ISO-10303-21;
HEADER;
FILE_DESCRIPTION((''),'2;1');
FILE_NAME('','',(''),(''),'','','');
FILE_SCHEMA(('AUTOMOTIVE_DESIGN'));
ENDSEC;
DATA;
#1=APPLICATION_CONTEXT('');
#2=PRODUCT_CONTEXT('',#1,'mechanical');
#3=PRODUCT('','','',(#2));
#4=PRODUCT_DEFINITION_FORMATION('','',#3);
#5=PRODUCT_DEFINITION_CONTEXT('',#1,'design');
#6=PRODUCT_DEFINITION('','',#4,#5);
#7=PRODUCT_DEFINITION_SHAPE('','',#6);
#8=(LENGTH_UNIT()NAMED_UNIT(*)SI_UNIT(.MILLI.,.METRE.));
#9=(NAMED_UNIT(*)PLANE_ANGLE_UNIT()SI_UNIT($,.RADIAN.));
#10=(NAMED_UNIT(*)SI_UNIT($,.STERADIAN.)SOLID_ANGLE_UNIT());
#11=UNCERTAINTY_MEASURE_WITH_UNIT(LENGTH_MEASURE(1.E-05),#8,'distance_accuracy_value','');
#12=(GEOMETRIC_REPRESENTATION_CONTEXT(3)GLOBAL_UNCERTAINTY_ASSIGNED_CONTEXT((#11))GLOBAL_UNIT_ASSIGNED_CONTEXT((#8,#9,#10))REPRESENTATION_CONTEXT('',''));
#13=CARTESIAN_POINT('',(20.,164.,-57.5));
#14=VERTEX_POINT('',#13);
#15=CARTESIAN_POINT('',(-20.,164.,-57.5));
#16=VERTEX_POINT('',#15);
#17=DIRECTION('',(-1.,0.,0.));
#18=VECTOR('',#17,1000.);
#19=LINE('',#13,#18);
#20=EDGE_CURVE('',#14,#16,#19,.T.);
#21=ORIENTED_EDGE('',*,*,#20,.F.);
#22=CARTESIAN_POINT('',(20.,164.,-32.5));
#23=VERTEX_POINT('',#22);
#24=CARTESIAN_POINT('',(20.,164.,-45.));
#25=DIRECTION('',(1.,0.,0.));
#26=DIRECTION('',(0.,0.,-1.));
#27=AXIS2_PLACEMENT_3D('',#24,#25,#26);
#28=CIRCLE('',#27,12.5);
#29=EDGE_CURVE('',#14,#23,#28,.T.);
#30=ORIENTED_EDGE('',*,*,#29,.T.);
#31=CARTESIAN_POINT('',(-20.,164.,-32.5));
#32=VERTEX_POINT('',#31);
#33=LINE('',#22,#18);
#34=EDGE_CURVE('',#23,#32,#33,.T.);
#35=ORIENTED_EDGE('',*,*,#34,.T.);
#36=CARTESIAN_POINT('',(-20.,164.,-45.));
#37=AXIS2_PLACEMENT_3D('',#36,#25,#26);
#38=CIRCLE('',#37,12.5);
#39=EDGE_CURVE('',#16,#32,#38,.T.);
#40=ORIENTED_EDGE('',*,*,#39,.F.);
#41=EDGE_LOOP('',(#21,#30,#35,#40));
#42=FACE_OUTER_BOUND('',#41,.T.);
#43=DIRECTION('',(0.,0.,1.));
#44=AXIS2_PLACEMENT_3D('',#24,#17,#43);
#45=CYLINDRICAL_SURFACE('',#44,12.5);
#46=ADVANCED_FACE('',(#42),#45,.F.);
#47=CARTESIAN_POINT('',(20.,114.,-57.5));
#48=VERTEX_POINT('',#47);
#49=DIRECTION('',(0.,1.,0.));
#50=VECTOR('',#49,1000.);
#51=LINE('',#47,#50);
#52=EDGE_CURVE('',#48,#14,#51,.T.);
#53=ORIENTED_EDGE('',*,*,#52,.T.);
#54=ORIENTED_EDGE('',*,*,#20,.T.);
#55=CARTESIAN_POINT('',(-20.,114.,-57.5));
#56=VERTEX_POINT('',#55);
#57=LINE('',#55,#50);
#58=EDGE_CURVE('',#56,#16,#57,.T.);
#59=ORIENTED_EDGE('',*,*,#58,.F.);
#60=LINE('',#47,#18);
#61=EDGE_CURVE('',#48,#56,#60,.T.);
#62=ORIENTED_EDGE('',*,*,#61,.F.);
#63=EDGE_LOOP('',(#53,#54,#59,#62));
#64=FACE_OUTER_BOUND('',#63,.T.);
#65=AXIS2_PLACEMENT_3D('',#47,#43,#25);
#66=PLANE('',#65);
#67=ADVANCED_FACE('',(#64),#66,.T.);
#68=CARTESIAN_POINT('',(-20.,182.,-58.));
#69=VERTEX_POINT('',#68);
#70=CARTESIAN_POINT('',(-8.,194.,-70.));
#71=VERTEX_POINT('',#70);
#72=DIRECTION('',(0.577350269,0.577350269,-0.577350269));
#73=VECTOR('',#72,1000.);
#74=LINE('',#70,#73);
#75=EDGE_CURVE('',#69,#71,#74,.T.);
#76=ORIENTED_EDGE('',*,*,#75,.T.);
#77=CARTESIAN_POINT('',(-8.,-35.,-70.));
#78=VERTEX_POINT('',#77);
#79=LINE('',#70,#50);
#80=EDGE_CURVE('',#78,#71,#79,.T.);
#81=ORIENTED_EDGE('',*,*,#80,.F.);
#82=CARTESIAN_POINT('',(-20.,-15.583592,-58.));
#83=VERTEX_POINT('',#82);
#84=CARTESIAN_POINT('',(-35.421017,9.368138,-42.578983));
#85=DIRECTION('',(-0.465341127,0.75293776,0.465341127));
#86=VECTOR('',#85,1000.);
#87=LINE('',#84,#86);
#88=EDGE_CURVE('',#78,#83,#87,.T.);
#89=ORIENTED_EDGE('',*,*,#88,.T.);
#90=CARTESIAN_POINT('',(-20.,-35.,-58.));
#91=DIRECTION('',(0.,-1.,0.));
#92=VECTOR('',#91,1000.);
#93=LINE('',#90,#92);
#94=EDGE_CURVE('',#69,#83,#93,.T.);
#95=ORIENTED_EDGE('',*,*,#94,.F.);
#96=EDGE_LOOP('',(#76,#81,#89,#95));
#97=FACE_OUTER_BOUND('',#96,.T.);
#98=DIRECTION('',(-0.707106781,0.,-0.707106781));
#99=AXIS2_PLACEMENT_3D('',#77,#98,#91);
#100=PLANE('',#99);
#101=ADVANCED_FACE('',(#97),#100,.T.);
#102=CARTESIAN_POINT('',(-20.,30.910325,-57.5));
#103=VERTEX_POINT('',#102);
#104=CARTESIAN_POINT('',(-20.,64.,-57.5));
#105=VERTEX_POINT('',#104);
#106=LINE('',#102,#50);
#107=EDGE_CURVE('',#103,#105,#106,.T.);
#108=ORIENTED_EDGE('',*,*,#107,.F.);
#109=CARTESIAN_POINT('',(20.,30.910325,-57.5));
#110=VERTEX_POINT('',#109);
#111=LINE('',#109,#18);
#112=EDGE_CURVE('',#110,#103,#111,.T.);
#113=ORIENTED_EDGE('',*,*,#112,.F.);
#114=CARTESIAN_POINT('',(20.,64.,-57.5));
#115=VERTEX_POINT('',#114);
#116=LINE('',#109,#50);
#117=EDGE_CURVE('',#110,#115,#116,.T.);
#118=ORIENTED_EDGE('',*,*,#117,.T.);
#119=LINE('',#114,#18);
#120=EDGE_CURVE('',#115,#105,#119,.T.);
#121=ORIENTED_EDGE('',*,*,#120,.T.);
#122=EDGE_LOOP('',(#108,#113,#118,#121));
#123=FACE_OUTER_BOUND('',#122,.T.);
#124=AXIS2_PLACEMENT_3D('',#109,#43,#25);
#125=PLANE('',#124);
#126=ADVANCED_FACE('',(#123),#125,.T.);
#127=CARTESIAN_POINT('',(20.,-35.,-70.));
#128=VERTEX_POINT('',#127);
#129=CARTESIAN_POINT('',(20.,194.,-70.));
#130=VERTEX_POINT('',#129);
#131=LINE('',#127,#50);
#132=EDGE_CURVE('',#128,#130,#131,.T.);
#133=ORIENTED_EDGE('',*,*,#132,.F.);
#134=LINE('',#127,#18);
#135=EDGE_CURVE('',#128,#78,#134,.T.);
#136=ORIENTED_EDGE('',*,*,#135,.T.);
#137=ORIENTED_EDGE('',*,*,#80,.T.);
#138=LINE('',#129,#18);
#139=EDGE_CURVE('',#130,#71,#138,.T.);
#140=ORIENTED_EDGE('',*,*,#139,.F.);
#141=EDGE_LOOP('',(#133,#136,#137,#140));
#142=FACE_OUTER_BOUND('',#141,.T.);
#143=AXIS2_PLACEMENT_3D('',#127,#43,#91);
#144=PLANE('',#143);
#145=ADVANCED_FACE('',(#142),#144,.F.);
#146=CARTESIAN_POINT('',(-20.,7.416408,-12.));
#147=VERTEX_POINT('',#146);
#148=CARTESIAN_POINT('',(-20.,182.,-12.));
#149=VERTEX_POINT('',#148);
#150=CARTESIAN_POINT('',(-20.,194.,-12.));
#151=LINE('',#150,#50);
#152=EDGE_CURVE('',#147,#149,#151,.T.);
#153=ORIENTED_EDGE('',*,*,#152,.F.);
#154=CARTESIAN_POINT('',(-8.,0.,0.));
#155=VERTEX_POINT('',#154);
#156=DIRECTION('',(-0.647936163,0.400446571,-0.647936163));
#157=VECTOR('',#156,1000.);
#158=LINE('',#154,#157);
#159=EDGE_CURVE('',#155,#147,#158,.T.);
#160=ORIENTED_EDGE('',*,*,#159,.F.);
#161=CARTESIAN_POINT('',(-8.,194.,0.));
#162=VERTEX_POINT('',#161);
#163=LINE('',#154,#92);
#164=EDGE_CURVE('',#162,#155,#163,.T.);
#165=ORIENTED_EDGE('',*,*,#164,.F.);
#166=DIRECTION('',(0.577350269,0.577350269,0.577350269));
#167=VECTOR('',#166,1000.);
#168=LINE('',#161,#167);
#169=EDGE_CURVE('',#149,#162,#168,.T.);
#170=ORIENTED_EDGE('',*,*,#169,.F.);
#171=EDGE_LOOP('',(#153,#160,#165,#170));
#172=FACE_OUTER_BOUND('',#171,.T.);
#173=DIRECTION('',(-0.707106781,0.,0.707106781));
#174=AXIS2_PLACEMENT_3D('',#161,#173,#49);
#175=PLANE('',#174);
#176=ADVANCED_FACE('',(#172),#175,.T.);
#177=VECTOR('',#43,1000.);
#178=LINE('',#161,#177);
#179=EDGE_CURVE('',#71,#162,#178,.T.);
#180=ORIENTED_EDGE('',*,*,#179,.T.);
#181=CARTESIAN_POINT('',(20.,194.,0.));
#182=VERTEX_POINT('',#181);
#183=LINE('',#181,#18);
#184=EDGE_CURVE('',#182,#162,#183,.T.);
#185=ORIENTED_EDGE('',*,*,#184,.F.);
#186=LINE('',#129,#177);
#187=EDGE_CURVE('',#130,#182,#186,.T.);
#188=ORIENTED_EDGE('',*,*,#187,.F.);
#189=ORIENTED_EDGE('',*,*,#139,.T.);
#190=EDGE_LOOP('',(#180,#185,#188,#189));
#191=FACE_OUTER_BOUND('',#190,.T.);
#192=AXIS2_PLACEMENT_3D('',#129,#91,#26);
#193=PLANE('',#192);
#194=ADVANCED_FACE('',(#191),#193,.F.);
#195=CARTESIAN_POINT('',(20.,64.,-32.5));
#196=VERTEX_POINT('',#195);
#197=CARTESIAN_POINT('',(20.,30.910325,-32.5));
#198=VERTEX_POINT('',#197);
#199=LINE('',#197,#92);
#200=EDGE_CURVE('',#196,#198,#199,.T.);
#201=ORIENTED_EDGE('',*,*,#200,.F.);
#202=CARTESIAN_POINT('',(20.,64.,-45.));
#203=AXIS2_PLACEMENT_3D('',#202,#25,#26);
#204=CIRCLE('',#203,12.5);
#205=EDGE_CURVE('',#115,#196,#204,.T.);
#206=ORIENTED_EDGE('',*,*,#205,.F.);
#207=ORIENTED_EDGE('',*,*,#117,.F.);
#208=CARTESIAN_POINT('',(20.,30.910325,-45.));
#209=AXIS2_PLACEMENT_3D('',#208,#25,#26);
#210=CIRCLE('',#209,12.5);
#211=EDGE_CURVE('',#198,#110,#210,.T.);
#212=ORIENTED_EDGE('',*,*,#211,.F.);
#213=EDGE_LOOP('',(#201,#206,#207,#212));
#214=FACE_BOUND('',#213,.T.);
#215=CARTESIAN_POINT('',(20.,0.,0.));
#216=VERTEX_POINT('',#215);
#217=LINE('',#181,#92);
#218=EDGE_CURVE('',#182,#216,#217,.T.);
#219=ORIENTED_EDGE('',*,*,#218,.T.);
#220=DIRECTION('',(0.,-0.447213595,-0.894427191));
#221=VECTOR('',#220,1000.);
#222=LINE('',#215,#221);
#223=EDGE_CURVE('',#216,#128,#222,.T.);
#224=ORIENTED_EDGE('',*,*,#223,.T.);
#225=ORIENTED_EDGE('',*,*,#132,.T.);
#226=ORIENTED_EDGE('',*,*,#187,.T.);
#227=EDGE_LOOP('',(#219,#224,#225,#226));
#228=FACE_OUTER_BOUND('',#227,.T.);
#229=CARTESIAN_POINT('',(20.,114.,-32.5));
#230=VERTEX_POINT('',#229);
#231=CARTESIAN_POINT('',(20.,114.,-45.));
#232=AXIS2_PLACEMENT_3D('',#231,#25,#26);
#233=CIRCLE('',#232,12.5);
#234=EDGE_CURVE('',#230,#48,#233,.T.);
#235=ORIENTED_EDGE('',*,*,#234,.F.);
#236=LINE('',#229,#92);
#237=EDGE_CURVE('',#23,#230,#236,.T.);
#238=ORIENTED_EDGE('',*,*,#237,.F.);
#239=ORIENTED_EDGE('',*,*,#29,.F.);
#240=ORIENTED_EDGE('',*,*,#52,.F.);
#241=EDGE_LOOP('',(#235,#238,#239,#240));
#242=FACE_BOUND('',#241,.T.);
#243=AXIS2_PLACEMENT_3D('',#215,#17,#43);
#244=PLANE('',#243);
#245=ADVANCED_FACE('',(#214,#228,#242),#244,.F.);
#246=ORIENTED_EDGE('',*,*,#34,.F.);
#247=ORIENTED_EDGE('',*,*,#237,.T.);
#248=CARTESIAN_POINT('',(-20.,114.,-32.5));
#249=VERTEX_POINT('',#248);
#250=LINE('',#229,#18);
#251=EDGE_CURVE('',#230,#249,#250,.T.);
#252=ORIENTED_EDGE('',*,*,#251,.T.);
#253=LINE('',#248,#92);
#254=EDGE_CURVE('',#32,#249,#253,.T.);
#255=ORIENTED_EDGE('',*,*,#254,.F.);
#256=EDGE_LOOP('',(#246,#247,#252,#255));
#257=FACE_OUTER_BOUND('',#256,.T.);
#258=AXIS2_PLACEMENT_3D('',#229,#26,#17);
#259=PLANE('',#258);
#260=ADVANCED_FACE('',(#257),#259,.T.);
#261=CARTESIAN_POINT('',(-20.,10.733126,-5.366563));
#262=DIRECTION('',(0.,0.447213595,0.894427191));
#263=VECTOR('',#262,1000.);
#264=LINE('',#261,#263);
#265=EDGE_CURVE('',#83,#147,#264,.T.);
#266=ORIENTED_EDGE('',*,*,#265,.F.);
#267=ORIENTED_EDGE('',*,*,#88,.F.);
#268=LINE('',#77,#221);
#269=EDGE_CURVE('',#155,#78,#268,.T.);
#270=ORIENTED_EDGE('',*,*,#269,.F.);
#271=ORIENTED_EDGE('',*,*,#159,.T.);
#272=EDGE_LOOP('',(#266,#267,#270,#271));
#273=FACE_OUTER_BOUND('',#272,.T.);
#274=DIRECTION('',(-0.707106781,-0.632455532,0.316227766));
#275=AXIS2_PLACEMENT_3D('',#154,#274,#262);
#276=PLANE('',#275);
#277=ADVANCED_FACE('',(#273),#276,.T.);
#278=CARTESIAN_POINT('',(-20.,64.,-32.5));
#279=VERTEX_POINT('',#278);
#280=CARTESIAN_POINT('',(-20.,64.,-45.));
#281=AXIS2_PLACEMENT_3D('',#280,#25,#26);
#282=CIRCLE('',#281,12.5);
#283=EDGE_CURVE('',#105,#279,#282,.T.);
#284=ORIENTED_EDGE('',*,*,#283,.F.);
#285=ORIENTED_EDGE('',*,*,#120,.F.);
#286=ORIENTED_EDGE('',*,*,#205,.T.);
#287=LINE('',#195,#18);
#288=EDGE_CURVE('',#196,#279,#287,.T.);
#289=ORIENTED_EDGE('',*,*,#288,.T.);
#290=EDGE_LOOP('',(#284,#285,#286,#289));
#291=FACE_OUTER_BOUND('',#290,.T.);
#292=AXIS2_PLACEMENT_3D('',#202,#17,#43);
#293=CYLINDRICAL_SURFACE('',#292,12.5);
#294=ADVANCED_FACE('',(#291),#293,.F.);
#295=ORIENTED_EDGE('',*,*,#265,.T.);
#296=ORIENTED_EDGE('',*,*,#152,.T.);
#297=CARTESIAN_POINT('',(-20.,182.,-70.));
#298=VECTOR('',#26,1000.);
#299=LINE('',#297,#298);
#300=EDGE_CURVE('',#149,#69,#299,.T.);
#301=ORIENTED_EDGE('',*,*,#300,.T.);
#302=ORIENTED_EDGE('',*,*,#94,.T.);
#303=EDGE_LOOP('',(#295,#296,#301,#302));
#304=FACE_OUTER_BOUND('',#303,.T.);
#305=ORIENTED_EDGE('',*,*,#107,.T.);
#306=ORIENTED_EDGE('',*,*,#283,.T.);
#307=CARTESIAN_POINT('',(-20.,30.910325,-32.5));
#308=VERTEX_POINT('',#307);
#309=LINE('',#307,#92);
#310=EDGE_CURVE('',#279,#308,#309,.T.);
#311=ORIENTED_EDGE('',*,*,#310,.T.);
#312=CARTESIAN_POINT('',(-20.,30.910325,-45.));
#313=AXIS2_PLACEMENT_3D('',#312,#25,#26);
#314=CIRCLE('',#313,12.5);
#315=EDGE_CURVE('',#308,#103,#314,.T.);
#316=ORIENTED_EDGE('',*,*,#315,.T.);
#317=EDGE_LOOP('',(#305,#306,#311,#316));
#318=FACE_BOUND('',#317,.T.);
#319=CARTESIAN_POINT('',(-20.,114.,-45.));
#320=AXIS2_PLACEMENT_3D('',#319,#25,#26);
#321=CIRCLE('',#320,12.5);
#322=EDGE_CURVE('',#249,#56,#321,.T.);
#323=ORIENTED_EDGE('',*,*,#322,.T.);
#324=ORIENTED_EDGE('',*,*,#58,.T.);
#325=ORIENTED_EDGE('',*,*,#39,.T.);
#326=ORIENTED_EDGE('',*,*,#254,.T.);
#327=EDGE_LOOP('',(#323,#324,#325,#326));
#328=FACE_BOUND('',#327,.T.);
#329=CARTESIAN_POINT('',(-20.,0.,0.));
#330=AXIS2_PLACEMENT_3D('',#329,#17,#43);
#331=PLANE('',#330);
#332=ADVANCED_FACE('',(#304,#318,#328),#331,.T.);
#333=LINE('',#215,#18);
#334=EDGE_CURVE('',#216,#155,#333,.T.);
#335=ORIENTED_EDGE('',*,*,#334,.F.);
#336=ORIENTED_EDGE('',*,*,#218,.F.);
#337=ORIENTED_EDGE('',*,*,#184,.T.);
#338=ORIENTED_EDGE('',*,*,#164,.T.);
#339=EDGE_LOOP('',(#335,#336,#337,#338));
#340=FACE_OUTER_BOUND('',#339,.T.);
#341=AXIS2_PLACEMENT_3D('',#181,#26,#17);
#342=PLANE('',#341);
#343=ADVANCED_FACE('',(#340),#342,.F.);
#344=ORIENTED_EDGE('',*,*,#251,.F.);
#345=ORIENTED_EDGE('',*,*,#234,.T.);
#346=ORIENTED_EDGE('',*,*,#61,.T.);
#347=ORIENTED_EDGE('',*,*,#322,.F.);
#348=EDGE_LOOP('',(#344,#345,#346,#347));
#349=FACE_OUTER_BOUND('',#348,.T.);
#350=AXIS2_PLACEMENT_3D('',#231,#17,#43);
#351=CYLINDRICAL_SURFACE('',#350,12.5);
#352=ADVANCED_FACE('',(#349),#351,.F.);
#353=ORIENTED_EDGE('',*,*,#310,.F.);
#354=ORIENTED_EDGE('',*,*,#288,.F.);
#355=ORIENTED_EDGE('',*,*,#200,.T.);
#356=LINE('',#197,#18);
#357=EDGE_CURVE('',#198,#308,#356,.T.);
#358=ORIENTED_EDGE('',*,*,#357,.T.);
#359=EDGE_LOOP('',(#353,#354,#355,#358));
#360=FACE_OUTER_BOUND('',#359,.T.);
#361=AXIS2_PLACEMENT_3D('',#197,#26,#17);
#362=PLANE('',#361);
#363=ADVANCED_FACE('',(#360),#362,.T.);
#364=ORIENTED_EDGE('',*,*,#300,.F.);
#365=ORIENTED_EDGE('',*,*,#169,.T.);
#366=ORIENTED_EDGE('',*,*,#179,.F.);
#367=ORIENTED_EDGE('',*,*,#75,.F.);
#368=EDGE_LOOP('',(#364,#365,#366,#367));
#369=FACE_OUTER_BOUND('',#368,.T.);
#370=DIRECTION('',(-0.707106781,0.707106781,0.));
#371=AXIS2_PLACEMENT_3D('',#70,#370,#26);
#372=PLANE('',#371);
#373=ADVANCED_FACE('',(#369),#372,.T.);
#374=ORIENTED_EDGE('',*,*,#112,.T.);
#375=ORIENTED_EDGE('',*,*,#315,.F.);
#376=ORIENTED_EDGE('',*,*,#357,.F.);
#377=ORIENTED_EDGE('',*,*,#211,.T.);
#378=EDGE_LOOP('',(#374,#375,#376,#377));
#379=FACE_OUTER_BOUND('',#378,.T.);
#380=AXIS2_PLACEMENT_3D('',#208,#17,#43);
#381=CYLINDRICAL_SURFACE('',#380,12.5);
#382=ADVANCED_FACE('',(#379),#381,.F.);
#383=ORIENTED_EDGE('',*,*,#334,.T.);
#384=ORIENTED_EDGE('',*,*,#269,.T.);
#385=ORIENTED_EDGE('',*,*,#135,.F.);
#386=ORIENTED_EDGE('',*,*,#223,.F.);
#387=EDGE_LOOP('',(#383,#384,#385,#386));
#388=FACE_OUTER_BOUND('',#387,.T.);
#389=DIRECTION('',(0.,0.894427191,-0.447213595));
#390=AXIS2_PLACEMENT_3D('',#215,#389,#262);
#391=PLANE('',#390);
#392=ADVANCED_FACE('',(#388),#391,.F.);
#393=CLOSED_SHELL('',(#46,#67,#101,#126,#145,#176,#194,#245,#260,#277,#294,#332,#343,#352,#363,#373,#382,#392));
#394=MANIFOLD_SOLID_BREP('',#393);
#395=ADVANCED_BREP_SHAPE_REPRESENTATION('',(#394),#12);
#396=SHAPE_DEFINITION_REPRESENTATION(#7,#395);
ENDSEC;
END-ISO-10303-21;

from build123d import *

# Parameters (mm, degrees)
BOSS_EXTRUDE1_DEPTH = 20
CHAMFER1_SIZE       = 12


with BuildPart() as part:
    # Sketch1 → Boss-Extrude1 (new, symmetric)
    with BuildSketch(Plane(origin=(0, 0, 0), x_dir=(0, 0, -1), z_dir=(1, 0, 0))):
        Polygon((0, 0), (70, -35), (70, 194), (0, 194), align=None)
        with BuildLine():
            Line((32.5, 114), (32.5, 164))
            ThreePointArc((32.5, 164), (45, 176.5), (57.5, 164))
            Line((57.5, 164), (57.5, 114))
            ThreePointArc((57.5, 114), (45, 101.5), (32.5, 114))
        make_face(mode=Mode.SUBTRACT)
        with BuildLine():
            Line((32.5, 30.910324642), (32.5, 64))
            ThreePointArc((32.5, 64), (45, 76.5), (57.5, 64))
            Line((57.5, 64), (57.5, 30.910324642))
            ThreePointArc((57.5, 30.910324642), (45, 18.410324642), (32.5, 30.910324642))
        make_face(mode=Mode.SUBTRACT)
    extrude(amount=BOSS_EXTRUDE1_DEPTH, both=True)

    # Chamfer1
    chamfer1_edges = [part.edges().sort_by_distance(p)[0] for p in [
        (-20, 194, -35),
        (-20, 79.5, -70),
        (-20, -17.5, -35),
        (-20, 97, 0),
    ]]
    chamfer(chamfer1_edges, length=CHAMFER1_SIZE)


solid = part.part
